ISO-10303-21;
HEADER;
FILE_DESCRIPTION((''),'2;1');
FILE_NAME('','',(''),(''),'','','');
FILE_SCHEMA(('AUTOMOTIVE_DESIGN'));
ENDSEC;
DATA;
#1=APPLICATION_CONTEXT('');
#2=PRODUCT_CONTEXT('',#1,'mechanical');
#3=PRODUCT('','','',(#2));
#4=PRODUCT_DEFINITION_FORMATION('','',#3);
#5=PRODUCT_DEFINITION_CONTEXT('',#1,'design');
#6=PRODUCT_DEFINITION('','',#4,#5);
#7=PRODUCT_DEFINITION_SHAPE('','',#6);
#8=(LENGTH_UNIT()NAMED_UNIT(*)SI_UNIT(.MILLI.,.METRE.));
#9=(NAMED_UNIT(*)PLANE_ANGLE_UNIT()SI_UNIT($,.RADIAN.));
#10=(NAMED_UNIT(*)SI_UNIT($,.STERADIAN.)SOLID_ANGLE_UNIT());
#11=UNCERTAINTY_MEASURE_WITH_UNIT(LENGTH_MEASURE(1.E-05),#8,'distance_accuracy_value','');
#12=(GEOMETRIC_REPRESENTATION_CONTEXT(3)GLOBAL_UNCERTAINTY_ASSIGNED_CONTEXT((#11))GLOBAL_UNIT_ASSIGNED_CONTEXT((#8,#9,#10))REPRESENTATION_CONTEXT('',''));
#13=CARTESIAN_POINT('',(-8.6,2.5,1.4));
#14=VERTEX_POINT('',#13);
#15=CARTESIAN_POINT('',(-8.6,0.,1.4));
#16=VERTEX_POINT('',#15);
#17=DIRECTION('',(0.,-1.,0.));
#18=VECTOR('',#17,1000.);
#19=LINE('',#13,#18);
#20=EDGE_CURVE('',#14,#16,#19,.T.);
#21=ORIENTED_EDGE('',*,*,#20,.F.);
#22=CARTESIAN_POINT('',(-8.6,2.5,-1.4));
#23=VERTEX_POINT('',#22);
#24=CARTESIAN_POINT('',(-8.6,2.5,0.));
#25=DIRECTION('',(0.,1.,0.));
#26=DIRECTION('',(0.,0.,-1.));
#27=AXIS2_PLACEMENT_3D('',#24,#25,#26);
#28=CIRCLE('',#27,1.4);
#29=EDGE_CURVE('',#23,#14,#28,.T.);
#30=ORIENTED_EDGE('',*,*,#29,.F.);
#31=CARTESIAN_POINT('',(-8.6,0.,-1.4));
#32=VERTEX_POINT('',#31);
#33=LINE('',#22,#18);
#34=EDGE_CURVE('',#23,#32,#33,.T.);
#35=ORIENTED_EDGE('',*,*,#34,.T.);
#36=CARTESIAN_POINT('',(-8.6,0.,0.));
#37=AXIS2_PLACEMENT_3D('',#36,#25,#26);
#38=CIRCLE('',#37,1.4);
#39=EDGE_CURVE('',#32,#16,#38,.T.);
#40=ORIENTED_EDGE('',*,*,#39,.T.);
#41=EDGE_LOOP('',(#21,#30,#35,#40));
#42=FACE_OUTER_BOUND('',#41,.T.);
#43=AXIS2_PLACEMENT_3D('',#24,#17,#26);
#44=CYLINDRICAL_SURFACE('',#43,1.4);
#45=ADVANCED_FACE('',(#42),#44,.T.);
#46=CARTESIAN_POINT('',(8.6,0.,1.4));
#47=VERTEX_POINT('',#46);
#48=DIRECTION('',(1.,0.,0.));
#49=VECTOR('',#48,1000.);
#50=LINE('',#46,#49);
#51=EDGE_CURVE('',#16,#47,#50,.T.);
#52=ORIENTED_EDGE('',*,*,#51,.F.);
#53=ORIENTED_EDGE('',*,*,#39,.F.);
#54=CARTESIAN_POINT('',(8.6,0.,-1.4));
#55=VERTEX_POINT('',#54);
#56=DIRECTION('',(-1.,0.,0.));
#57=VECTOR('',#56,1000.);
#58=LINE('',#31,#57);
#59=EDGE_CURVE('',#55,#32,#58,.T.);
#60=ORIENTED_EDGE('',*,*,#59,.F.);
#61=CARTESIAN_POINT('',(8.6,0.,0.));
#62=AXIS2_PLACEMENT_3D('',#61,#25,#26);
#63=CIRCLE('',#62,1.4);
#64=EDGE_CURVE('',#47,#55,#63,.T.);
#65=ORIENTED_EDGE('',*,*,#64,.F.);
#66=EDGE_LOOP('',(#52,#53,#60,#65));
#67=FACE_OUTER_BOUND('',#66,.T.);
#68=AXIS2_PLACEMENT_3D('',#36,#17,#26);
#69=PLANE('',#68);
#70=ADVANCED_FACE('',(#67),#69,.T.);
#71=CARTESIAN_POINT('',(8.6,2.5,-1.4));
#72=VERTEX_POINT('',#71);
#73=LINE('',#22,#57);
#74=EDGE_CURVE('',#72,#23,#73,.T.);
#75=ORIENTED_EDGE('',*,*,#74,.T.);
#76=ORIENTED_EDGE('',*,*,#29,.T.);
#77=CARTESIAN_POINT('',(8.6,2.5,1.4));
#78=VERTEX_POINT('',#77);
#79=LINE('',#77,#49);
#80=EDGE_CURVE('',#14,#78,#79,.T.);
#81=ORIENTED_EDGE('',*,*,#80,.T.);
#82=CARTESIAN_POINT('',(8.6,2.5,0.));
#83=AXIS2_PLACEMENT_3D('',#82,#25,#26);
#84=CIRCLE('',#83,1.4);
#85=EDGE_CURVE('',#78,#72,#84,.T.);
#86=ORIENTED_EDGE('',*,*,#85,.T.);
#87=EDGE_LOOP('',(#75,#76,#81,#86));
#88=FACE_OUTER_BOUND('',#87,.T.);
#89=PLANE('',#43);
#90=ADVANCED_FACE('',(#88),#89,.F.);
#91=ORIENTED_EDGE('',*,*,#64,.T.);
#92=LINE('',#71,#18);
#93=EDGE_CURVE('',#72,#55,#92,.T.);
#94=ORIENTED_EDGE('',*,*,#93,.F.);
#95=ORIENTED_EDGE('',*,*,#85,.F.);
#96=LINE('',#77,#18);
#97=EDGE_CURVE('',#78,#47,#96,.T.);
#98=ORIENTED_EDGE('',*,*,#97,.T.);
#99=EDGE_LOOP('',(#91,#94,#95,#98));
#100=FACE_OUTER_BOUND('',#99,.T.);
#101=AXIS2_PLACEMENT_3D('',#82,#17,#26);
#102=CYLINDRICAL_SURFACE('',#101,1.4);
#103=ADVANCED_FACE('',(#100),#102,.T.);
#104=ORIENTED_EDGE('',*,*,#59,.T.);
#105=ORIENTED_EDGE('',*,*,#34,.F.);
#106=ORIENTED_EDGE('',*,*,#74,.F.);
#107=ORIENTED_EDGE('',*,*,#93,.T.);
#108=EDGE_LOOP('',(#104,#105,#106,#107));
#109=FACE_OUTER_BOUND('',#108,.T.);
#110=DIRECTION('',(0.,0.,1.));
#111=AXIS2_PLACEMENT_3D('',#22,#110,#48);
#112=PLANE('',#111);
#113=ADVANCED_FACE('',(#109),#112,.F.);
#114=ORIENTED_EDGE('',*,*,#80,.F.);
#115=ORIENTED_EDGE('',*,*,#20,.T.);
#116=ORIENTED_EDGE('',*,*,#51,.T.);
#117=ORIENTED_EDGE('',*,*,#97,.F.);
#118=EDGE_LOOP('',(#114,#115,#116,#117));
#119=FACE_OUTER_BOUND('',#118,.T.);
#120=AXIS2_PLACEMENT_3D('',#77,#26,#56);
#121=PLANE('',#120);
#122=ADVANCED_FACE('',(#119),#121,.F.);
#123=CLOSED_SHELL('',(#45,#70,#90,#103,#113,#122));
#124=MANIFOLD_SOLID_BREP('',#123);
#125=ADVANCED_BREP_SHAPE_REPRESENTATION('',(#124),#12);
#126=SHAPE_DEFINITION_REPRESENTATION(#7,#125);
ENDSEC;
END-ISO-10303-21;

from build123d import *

# Parameters (mm, degrees)
BOSS_EXTRUDE1_DEPTH = 2.5


with BuildPart() as part:
    # Sketch1 → Boss-Extrude1 (new body)
    with BuildSketch(Plane(origin=(0, 0, 0), x_dir=(1, 0, 0), z_dir=(0, 1, 0))):
        with BuildLine():
            Line((-8.6, 1.4), (8.6, 1.4))
            ThreePointArc((8.6, 1.4), (10, 0), (8.6, -1.4))
            Line((8.6, -1.4), (-8.6, -1.4))
            ThreePointArc((-8.6, -1.4), (-10, 0), (-8.6, 1.4))
        make_face()
    extrude(amount=BOSS_EXTRUDE1_DEPTH)


solid = part.part
